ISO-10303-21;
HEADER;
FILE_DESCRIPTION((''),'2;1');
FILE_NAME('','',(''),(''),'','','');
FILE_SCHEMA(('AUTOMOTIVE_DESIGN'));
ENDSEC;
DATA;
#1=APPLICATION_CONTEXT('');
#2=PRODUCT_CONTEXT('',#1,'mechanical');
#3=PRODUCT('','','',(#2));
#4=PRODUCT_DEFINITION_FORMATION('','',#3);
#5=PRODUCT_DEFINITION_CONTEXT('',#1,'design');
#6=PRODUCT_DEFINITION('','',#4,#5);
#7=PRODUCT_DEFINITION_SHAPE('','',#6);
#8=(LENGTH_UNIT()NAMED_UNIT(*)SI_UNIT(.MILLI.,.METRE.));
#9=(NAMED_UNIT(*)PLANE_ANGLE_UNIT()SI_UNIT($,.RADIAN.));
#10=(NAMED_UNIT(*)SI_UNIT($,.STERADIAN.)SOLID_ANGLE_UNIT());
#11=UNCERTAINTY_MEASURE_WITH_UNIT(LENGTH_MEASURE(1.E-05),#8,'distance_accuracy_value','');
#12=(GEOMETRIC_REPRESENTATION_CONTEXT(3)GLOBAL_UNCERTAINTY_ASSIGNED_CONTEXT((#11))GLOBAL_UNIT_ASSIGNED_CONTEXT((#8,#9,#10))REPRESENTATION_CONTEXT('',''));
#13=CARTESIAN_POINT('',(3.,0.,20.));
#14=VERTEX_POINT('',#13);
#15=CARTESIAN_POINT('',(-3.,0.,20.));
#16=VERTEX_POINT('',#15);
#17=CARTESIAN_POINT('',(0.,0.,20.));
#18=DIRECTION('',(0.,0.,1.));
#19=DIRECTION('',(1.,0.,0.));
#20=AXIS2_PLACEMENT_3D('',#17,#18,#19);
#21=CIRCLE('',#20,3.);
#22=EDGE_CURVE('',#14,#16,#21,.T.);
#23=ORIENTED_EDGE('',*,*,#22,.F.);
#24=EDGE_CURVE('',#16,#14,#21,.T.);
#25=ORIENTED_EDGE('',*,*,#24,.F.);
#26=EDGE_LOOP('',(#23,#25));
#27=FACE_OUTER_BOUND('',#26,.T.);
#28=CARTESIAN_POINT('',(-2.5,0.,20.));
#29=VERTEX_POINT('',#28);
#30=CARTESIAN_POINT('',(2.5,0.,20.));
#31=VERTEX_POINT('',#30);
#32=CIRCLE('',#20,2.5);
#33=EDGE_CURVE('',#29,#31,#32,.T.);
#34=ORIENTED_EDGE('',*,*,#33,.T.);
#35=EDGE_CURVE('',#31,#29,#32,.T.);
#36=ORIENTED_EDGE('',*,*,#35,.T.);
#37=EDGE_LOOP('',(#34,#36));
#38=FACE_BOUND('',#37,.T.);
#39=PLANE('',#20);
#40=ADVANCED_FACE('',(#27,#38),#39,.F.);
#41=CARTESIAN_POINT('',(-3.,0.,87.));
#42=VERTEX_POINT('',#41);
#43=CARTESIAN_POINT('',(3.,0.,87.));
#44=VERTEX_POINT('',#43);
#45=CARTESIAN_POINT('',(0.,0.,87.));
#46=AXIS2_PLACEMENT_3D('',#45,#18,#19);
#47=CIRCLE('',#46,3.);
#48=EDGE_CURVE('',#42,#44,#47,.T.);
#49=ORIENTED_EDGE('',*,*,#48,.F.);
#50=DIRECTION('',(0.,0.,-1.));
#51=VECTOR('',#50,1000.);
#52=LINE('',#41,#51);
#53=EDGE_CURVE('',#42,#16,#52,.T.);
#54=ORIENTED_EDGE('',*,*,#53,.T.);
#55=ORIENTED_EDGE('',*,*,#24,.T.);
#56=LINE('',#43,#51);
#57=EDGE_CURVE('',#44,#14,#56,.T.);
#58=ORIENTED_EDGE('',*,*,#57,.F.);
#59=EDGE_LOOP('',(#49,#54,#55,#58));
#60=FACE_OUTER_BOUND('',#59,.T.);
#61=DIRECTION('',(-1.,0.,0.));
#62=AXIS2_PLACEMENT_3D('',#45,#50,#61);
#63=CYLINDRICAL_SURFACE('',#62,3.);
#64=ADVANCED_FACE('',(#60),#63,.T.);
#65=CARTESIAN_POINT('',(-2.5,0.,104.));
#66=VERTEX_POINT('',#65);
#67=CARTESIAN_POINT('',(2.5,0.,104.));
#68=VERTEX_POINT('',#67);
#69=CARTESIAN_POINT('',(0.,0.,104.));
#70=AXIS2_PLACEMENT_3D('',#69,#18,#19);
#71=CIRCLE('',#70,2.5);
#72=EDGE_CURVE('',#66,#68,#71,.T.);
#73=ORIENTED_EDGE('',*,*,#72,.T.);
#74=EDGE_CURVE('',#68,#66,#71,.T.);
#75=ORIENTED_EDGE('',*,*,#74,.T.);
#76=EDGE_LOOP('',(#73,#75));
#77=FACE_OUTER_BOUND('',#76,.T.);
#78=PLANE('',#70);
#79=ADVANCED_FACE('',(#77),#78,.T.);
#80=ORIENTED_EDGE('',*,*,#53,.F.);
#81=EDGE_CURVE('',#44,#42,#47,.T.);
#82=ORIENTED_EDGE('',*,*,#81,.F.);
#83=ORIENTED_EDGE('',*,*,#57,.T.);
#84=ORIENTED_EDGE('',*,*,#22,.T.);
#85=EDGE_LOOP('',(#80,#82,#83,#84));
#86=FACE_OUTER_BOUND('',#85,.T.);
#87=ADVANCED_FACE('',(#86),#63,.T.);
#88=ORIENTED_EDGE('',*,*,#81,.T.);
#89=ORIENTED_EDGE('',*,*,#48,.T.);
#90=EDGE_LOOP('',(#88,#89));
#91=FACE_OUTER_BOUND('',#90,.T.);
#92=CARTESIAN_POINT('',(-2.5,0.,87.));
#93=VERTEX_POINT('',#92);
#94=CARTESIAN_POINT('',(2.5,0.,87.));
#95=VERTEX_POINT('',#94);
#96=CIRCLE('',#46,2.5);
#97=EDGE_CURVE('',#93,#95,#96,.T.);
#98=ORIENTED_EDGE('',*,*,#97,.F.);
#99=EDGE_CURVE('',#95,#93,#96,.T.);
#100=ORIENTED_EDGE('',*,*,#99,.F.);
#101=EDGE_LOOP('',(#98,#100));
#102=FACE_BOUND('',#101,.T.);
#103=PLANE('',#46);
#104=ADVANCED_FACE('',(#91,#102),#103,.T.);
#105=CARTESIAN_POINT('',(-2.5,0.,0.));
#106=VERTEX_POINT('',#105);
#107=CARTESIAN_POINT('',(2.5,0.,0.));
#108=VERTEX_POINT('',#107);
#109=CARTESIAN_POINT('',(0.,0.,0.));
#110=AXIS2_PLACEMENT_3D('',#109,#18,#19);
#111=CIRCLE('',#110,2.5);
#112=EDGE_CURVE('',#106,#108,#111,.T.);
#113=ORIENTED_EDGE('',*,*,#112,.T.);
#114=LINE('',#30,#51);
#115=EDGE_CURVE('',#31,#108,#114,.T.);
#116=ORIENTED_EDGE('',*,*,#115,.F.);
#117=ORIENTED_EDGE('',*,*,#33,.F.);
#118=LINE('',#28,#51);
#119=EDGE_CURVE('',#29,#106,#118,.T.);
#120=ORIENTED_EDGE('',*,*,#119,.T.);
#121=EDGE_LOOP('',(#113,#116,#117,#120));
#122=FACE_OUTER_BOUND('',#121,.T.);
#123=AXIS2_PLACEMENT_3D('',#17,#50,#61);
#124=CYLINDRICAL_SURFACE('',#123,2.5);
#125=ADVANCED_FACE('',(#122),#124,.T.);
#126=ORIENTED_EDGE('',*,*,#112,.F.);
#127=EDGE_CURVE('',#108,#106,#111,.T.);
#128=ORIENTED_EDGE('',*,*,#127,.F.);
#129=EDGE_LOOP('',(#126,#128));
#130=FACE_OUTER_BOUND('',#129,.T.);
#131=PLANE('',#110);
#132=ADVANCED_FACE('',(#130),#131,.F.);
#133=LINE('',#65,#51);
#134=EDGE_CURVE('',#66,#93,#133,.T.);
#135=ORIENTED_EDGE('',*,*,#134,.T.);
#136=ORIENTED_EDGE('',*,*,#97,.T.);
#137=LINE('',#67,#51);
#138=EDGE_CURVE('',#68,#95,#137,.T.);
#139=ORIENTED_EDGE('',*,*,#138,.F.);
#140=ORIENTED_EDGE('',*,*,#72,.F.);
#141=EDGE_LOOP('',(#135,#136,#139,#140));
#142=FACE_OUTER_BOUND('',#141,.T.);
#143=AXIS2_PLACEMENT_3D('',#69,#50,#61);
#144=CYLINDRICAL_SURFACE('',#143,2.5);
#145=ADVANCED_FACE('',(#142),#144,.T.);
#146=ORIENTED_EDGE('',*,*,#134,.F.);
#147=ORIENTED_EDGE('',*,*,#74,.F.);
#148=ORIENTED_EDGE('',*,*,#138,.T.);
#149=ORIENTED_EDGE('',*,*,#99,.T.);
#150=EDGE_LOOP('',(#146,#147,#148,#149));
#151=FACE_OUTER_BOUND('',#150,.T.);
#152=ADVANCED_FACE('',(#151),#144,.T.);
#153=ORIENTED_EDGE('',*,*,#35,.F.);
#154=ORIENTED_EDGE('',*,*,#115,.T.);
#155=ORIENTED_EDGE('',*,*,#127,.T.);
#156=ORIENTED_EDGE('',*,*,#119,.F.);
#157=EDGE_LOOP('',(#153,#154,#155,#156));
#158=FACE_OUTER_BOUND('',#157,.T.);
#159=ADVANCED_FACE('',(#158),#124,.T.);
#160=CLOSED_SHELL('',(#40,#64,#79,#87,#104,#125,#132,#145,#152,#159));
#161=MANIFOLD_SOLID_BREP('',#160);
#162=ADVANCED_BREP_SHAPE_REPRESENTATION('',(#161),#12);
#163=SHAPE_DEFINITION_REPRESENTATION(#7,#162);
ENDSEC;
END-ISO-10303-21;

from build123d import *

# Parameters (mm, degrees)
SKETCH1_R           = 2.5
BOSS_EXTRUDE1_DEPTH = 20
SKETCH2_R           = 3
BOSS_EXTRUDE2_DEPTH = 67
SKETCH3_R           = 2.5
BOSS_EXTRUDE3_DEPTH = 17


with BuildPart() as part:
    # Sketch1 → Boss-Extrude1 (new body)
    with BuildSketch(Plane.XY):
        Circle(SKETCH1_R)
    extrude(amount=BOSS_EXTRUDE1_DEPTH)

    # Sketch2 → Boss-Extrude2 (add)
    with BuildSketch(Plane.XY.offset(20)):
        Circle(SKETCH2_R)
    extrude(amount=BOSS_EXTRUDE2_DEPTH)

    # Sketch3 → Boss-Extrude3 (add)
    with BuildSketch(Plane.XY.offset(87)):
        Circle(SKETCH3_R)
    extrude(amount=BOSS_EXTRUDE3_DEPTH)


solid = part.part
